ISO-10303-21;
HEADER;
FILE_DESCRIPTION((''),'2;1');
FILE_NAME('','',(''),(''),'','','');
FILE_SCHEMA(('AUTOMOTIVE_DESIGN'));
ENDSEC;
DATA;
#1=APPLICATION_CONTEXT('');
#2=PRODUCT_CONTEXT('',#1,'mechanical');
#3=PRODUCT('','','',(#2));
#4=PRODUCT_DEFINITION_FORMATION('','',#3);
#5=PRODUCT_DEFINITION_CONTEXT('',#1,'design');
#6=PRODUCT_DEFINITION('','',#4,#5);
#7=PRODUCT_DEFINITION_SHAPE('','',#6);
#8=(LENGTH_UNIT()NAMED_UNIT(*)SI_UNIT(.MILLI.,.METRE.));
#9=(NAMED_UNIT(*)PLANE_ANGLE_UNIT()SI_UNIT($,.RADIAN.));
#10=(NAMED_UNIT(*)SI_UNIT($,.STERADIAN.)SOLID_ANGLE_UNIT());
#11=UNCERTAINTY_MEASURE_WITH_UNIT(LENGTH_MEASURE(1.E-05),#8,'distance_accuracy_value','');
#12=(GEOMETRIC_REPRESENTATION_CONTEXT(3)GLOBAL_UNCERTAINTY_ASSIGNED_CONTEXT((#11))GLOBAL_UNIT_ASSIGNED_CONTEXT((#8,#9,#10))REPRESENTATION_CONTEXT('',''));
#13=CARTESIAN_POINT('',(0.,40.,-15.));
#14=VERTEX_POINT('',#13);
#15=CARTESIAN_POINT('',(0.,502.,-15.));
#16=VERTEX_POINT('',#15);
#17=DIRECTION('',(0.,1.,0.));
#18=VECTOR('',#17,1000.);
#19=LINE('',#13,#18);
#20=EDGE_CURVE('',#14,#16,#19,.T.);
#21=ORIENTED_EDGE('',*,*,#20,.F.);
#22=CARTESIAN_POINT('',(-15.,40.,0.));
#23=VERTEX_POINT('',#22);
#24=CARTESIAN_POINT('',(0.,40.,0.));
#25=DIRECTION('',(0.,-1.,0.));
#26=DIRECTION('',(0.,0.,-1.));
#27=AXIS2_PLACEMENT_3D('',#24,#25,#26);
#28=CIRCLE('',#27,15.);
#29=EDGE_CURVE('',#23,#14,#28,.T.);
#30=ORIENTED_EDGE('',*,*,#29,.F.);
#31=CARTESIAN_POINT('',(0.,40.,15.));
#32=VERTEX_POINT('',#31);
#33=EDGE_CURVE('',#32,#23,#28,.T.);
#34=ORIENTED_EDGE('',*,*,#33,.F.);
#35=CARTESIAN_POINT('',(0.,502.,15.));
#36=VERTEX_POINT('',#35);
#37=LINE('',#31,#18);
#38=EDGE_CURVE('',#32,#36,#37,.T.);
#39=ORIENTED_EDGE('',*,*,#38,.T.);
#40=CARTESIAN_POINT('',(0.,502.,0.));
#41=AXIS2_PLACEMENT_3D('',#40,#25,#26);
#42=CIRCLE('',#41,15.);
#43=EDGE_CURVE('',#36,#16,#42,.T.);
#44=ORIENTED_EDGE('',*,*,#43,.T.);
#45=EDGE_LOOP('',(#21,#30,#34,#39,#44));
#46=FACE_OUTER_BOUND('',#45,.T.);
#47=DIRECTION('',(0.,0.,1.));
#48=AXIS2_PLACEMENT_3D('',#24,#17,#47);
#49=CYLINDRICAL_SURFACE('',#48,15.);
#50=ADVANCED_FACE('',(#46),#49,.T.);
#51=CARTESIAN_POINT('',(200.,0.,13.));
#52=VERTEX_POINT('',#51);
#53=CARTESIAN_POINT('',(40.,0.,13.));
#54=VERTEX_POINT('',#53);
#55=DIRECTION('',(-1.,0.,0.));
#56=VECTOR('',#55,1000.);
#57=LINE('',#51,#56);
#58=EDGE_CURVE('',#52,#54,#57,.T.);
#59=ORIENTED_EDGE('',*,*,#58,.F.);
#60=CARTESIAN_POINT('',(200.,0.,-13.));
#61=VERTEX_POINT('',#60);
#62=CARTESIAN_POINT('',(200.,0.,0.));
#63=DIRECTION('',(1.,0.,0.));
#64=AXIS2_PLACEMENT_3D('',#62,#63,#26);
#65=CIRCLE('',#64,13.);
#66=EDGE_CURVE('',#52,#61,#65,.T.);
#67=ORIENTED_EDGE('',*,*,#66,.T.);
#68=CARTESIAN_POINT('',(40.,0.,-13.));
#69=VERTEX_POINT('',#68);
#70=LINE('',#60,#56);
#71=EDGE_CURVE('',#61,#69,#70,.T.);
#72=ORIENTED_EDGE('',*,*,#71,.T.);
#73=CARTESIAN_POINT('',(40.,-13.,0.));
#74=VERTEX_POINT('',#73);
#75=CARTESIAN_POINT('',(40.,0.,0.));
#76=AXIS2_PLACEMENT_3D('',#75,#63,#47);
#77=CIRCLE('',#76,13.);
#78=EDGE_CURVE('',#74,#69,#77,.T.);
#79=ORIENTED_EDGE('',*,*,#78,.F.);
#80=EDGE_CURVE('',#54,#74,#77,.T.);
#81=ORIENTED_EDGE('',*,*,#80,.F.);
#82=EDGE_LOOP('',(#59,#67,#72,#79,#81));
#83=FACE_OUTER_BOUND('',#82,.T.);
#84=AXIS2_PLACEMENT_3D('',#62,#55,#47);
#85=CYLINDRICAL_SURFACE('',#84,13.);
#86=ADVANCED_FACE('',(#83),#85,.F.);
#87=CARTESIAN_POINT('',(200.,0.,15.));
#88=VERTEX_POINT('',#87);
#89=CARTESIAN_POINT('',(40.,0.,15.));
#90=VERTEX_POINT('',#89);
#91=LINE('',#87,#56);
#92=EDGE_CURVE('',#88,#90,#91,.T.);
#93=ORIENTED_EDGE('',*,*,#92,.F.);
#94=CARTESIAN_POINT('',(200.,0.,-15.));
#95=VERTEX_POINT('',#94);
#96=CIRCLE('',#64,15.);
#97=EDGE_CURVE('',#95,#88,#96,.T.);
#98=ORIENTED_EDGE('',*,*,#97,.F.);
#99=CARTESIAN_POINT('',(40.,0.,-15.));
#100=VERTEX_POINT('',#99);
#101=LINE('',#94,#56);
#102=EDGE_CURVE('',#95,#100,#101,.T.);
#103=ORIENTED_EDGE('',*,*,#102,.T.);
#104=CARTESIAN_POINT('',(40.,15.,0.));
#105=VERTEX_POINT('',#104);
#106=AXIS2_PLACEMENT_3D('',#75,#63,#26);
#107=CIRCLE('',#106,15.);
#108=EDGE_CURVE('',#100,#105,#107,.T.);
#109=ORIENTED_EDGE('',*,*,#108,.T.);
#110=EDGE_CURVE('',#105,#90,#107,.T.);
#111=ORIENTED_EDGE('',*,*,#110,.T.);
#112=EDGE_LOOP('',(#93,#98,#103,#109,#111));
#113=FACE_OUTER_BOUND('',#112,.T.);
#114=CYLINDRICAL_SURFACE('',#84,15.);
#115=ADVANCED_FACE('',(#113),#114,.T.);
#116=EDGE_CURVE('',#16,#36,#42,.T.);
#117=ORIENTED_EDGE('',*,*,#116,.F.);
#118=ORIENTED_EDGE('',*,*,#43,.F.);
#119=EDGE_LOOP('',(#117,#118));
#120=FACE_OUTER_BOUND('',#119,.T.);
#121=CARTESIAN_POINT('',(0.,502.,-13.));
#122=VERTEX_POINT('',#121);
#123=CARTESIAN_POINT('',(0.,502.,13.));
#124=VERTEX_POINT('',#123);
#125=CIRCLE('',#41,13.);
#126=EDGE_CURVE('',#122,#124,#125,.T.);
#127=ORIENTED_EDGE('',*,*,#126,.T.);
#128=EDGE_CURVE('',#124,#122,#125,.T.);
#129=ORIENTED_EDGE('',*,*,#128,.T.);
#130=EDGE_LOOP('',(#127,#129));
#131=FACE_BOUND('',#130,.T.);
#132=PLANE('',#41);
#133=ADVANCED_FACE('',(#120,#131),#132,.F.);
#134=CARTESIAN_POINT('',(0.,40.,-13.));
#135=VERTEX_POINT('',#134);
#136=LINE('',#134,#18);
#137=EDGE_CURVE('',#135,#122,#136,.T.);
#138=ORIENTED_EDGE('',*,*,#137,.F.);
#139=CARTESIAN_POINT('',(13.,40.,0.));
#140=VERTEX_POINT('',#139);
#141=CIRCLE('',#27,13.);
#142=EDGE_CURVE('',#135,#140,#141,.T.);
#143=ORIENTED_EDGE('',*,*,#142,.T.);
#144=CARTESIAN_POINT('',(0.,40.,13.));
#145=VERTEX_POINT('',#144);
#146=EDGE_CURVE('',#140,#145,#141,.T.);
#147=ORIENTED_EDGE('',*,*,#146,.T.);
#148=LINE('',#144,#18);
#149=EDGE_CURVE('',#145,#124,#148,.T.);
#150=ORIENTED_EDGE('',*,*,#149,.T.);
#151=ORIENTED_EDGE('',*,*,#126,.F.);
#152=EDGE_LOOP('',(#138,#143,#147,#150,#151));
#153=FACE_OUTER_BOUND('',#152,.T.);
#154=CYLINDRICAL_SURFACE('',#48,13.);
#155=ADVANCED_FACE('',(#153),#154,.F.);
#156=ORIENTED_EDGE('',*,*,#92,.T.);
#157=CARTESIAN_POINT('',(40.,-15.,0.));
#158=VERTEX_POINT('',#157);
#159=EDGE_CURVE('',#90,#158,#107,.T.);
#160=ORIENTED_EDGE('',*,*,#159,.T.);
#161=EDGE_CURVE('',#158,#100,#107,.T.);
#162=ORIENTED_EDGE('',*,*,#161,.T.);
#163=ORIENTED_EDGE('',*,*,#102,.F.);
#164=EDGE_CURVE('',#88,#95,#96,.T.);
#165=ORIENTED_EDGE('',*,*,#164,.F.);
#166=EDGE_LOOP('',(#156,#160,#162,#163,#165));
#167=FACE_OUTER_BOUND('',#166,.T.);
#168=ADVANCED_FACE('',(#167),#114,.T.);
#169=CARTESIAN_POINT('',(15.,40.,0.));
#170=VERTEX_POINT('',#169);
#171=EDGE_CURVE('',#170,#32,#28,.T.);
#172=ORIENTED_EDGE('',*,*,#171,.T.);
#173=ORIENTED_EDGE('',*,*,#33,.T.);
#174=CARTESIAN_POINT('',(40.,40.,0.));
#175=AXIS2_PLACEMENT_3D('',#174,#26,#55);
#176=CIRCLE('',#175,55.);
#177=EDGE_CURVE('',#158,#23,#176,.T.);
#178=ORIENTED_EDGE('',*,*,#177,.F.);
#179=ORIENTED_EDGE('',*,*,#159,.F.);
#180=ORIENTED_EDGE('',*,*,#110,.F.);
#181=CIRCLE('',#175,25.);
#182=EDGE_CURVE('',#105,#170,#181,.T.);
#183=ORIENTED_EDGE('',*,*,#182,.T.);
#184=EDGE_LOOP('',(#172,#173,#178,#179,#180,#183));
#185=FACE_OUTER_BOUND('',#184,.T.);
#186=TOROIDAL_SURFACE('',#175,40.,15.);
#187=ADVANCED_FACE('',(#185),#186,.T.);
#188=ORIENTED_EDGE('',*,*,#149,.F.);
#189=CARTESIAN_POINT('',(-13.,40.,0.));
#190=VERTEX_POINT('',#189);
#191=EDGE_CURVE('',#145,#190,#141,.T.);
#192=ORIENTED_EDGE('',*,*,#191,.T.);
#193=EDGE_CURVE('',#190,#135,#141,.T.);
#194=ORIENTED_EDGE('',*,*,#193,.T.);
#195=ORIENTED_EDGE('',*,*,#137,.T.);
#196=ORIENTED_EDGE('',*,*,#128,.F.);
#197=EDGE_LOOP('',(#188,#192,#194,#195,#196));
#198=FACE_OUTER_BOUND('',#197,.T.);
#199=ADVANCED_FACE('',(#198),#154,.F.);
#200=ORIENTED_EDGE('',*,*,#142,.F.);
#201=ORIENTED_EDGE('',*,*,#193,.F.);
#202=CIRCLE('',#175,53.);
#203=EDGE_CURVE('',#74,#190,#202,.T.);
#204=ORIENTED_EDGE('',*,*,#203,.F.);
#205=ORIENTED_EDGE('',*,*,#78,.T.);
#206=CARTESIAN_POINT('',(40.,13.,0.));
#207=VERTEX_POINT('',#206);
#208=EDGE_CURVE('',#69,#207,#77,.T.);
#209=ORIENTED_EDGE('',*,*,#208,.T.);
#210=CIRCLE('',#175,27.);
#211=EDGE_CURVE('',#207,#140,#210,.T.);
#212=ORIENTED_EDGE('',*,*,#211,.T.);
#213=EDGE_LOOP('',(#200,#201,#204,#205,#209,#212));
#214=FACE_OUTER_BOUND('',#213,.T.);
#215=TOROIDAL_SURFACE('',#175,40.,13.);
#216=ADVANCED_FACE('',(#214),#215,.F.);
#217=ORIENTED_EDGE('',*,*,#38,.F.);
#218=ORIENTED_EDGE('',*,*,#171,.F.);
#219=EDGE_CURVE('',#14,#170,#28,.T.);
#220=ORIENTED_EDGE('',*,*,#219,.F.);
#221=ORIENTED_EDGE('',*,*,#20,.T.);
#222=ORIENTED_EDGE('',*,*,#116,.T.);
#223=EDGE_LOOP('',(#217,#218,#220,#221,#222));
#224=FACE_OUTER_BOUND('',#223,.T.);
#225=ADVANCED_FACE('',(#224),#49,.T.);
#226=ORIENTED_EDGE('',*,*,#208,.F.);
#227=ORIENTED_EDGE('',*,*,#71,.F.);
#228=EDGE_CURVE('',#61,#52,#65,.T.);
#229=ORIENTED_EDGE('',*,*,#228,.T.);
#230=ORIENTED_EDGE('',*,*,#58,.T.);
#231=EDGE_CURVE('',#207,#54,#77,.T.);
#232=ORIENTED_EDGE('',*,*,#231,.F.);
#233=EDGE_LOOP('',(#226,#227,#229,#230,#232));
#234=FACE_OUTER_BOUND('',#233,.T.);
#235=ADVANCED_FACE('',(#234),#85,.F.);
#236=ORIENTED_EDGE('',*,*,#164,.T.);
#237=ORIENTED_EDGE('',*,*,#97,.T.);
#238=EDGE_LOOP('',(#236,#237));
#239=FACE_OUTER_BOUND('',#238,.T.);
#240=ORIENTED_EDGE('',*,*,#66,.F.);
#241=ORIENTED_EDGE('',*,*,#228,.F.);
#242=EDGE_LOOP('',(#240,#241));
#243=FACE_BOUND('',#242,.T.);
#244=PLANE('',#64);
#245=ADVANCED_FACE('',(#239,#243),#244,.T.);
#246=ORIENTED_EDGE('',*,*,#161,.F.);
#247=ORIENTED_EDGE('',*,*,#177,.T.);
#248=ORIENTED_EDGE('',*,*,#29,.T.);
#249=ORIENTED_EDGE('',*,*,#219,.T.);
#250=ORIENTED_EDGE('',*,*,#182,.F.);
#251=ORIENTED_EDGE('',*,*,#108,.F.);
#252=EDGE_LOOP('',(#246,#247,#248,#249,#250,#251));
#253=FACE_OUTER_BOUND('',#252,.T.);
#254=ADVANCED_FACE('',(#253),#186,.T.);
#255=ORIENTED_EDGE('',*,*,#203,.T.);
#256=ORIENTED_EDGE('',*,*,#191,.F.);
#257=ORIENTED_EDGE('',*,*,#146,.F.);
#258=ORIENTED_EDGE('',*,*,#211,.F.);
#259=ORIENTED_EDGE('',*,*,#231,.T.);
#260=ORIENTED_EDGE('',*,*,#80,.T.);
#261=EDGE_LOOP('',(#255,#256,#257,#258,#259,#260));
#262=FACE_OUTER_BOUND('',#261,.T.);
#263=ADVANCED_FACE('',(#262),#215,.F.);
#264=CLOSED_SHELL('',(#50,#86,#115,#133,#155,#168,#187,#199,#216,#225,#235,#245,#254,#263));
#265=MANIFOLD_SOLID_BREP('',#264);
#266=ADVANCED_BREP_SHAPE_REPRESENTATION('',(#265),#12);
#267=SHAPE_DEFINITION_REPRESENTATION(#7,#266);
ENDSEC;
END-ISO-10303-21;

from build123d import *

# Parameters (mm, degrees)
SWEEP_THIN1_PROFILE_R   = 15
SWEEP_THIN1_PROFILE_R_2 = 13


with BuildPart() as part:
    # Sweep-Thin1: sweep along a path in Sketch1
    with BuildLine(Plane.XY) as sweep_thin1_path:
        Line((200, 0), (40, 0))
        ThreePointArc((40, 0), (11.715728753, 11.715728753), (0, 40))
        Line((0, 40), (0, 502))
    # Sweep-Thin1 profile (on start of the path) → Sweep-Thin1 (sweep)
    with BuildSketch(Plane(origin=(200, 0, 0), x_dir=(0, 0, -1), z_dir=(-1, 0, 0))):
        Circle(SWEEP_THIN1_PROFILE_R)
        Circle(SWEEP_THIN1_PROFILE_R_2, mode=Mode.SUBTRACT)
    sweep(path=sweep_thin1_path.line)


solid = part.part
